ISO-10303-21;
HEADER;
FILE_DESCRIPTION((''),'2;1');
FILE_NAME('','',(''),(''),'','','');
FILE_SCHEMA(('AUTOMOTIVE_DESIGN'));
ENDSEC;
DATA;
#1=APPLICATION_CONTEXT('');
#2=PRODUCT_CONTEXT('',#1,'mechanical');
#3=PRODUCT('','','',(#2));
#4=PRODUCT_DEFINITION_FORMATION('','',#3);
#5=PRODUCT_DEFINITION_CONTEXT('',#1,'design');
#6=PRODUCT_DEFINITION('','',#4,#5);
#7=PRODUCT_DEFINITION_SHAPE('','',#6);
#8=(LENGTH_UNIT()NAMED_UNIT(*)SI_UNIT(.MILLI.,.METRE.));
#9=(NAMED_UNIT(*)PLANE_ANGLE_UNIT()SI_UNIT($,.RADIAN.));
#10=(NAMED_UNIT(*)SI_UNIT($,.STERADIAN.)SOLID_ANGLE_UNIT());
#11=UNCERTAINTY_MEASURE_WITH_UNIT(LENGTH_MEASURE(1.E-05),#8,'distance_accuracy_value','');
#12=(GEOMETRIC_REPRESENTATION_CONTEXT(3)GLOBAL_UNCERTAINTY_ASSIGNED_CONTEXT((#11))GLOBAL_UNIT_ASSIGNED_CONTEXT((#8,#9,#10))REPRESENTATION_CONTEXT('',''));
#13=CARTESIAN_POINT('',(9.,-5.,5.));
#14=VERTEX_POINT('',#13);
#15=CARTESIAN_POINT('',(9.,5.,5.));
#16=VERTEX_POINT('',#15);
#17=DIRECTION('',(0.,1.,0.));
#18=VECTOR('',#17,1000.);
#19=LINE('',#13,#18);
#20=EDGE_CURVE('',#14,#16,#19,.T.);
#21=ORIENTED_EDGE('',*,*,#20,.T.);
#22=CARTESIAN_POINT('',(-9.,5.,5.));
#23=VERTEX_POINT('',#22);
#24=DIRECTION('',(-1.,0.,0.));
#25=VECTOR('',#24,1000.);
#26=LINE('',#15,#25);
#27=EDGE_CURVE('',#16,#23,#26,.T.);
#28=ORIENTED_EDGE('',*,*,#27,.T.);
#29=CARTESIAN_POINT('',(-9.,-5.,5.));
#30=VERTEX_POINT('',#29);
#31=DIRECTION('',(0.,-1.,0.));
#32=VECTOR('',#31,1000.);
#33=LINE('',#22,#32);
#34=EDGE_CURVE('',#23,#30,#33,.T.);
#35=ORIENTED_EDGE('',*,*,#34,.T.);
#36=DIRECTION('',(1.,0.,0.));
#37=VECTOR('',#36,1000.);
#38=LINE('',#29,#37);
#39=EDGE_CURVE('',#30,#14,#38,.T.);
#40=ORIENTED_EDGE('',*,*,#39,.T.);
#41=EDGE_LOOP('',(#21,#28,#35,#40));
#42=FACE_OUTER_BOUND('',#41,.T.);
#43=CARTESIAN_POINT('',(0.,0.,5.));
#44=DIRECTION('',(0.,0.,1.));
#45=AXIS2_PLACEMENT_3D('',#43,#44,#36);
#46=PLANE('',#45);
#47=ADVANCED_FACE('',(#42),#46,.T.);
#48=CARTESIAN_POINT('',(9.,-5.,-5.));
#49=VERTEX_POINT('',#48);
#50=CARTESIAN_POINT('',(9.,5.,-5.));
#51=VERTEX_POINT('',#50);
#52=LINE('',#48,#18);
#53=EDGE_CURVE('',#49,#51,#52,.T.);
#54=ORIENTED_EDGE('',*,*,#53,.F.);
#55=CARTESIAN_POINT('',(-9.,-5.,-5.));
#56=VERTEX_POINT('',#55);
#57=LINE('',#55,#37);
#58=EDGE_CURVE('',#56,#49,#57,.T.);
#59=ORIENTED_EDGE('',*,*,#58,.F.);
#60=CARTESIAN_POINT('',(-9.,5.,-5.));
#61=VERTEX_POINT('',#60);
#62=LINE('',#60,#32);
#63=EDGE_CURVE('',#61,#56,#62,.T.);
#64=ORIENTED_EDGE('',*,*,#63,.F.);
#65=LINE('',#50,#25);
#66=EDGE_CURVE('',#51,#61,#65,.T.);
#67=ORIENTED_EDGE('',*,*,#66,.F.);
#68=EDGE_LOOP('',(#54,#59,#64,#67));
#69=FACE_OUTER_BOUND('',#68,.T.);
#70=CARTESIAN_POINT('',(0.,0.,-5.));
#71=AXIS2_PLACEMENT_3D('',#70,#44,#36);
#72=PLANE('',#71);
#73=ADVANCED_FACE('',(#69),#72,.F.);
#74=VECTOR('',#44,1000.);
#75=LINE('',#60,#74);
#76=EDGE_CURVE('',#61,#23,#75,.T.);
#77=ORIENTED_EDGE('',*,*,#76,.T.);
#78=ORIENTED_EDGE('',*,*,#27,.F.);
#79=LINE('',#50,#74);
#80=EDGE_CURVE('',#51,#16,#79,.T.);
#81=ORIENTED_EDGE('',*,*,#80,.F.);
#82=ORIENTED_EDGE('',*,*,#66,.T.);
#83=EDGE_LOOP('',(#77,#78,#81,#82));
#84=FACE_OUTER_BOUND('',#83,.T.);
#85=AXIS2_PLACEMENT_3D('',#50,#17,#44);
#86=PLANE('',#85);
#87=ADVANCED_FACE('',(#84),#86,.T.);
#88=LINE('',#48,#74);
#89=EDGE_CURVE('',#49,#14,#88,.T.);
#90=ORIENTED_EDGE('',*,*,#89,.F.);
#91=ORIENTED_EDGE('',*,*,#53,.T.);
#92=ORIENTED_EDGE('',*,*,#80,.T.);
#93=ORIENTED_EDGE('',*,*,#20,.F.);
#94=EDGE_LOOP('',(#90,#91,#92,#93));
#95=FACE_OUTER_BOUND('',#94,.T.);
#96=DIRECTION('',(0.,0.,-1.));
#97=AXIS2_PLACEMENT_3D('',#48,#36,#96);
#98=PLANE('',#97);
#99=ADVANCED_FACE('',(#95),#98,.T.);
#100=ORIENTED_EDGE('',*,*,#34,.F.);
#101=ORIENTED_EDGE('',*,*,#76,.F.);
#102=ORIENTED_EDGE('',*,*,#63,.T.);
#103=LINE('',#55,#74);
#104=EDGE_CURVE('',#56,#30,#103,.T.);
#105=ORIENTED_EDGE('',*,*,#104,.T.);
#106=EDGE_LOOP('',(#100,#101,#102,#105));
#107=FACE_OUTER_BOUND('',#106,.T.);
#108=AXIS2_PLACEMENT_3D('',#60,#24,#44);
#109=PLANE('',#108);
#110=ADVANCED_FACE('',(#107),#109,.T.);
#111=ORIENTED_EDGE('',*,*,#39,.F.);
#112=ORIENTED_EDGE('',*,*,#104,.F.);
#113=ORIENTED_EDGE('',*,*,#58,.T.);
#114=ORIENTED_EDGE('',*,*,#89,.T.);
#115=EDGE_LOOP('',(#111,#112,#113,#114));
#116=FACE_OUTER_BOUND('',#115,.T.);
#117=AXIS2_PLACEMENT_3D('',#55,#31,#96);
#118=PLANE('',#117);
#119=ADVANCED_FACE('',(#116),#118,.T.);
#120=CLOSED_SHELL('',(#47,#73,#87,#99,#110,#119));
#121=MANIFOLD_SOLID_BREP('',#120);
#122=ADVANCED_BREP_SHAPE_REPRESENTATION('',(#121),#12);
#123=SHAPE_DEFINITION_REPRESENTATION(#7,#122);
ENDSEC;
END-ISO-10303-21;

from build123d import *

# Parameters (mm, degrees)
SKETCH_1_W      = 18
SKETCH_1_H      = 10
EXTRUDE_1_DEPTH = 5


with BuildPart() as part:
    # 草图1 → 凸台-拉伸1 (new, symmetric)
    with BuildSketch(Plane.XY):
        Rectangle(SKETCH_1_W, SKETCH_1_H)
    extrude(amount=EXTRUDE_1_DEPTH, both=True)


solid = part.part
